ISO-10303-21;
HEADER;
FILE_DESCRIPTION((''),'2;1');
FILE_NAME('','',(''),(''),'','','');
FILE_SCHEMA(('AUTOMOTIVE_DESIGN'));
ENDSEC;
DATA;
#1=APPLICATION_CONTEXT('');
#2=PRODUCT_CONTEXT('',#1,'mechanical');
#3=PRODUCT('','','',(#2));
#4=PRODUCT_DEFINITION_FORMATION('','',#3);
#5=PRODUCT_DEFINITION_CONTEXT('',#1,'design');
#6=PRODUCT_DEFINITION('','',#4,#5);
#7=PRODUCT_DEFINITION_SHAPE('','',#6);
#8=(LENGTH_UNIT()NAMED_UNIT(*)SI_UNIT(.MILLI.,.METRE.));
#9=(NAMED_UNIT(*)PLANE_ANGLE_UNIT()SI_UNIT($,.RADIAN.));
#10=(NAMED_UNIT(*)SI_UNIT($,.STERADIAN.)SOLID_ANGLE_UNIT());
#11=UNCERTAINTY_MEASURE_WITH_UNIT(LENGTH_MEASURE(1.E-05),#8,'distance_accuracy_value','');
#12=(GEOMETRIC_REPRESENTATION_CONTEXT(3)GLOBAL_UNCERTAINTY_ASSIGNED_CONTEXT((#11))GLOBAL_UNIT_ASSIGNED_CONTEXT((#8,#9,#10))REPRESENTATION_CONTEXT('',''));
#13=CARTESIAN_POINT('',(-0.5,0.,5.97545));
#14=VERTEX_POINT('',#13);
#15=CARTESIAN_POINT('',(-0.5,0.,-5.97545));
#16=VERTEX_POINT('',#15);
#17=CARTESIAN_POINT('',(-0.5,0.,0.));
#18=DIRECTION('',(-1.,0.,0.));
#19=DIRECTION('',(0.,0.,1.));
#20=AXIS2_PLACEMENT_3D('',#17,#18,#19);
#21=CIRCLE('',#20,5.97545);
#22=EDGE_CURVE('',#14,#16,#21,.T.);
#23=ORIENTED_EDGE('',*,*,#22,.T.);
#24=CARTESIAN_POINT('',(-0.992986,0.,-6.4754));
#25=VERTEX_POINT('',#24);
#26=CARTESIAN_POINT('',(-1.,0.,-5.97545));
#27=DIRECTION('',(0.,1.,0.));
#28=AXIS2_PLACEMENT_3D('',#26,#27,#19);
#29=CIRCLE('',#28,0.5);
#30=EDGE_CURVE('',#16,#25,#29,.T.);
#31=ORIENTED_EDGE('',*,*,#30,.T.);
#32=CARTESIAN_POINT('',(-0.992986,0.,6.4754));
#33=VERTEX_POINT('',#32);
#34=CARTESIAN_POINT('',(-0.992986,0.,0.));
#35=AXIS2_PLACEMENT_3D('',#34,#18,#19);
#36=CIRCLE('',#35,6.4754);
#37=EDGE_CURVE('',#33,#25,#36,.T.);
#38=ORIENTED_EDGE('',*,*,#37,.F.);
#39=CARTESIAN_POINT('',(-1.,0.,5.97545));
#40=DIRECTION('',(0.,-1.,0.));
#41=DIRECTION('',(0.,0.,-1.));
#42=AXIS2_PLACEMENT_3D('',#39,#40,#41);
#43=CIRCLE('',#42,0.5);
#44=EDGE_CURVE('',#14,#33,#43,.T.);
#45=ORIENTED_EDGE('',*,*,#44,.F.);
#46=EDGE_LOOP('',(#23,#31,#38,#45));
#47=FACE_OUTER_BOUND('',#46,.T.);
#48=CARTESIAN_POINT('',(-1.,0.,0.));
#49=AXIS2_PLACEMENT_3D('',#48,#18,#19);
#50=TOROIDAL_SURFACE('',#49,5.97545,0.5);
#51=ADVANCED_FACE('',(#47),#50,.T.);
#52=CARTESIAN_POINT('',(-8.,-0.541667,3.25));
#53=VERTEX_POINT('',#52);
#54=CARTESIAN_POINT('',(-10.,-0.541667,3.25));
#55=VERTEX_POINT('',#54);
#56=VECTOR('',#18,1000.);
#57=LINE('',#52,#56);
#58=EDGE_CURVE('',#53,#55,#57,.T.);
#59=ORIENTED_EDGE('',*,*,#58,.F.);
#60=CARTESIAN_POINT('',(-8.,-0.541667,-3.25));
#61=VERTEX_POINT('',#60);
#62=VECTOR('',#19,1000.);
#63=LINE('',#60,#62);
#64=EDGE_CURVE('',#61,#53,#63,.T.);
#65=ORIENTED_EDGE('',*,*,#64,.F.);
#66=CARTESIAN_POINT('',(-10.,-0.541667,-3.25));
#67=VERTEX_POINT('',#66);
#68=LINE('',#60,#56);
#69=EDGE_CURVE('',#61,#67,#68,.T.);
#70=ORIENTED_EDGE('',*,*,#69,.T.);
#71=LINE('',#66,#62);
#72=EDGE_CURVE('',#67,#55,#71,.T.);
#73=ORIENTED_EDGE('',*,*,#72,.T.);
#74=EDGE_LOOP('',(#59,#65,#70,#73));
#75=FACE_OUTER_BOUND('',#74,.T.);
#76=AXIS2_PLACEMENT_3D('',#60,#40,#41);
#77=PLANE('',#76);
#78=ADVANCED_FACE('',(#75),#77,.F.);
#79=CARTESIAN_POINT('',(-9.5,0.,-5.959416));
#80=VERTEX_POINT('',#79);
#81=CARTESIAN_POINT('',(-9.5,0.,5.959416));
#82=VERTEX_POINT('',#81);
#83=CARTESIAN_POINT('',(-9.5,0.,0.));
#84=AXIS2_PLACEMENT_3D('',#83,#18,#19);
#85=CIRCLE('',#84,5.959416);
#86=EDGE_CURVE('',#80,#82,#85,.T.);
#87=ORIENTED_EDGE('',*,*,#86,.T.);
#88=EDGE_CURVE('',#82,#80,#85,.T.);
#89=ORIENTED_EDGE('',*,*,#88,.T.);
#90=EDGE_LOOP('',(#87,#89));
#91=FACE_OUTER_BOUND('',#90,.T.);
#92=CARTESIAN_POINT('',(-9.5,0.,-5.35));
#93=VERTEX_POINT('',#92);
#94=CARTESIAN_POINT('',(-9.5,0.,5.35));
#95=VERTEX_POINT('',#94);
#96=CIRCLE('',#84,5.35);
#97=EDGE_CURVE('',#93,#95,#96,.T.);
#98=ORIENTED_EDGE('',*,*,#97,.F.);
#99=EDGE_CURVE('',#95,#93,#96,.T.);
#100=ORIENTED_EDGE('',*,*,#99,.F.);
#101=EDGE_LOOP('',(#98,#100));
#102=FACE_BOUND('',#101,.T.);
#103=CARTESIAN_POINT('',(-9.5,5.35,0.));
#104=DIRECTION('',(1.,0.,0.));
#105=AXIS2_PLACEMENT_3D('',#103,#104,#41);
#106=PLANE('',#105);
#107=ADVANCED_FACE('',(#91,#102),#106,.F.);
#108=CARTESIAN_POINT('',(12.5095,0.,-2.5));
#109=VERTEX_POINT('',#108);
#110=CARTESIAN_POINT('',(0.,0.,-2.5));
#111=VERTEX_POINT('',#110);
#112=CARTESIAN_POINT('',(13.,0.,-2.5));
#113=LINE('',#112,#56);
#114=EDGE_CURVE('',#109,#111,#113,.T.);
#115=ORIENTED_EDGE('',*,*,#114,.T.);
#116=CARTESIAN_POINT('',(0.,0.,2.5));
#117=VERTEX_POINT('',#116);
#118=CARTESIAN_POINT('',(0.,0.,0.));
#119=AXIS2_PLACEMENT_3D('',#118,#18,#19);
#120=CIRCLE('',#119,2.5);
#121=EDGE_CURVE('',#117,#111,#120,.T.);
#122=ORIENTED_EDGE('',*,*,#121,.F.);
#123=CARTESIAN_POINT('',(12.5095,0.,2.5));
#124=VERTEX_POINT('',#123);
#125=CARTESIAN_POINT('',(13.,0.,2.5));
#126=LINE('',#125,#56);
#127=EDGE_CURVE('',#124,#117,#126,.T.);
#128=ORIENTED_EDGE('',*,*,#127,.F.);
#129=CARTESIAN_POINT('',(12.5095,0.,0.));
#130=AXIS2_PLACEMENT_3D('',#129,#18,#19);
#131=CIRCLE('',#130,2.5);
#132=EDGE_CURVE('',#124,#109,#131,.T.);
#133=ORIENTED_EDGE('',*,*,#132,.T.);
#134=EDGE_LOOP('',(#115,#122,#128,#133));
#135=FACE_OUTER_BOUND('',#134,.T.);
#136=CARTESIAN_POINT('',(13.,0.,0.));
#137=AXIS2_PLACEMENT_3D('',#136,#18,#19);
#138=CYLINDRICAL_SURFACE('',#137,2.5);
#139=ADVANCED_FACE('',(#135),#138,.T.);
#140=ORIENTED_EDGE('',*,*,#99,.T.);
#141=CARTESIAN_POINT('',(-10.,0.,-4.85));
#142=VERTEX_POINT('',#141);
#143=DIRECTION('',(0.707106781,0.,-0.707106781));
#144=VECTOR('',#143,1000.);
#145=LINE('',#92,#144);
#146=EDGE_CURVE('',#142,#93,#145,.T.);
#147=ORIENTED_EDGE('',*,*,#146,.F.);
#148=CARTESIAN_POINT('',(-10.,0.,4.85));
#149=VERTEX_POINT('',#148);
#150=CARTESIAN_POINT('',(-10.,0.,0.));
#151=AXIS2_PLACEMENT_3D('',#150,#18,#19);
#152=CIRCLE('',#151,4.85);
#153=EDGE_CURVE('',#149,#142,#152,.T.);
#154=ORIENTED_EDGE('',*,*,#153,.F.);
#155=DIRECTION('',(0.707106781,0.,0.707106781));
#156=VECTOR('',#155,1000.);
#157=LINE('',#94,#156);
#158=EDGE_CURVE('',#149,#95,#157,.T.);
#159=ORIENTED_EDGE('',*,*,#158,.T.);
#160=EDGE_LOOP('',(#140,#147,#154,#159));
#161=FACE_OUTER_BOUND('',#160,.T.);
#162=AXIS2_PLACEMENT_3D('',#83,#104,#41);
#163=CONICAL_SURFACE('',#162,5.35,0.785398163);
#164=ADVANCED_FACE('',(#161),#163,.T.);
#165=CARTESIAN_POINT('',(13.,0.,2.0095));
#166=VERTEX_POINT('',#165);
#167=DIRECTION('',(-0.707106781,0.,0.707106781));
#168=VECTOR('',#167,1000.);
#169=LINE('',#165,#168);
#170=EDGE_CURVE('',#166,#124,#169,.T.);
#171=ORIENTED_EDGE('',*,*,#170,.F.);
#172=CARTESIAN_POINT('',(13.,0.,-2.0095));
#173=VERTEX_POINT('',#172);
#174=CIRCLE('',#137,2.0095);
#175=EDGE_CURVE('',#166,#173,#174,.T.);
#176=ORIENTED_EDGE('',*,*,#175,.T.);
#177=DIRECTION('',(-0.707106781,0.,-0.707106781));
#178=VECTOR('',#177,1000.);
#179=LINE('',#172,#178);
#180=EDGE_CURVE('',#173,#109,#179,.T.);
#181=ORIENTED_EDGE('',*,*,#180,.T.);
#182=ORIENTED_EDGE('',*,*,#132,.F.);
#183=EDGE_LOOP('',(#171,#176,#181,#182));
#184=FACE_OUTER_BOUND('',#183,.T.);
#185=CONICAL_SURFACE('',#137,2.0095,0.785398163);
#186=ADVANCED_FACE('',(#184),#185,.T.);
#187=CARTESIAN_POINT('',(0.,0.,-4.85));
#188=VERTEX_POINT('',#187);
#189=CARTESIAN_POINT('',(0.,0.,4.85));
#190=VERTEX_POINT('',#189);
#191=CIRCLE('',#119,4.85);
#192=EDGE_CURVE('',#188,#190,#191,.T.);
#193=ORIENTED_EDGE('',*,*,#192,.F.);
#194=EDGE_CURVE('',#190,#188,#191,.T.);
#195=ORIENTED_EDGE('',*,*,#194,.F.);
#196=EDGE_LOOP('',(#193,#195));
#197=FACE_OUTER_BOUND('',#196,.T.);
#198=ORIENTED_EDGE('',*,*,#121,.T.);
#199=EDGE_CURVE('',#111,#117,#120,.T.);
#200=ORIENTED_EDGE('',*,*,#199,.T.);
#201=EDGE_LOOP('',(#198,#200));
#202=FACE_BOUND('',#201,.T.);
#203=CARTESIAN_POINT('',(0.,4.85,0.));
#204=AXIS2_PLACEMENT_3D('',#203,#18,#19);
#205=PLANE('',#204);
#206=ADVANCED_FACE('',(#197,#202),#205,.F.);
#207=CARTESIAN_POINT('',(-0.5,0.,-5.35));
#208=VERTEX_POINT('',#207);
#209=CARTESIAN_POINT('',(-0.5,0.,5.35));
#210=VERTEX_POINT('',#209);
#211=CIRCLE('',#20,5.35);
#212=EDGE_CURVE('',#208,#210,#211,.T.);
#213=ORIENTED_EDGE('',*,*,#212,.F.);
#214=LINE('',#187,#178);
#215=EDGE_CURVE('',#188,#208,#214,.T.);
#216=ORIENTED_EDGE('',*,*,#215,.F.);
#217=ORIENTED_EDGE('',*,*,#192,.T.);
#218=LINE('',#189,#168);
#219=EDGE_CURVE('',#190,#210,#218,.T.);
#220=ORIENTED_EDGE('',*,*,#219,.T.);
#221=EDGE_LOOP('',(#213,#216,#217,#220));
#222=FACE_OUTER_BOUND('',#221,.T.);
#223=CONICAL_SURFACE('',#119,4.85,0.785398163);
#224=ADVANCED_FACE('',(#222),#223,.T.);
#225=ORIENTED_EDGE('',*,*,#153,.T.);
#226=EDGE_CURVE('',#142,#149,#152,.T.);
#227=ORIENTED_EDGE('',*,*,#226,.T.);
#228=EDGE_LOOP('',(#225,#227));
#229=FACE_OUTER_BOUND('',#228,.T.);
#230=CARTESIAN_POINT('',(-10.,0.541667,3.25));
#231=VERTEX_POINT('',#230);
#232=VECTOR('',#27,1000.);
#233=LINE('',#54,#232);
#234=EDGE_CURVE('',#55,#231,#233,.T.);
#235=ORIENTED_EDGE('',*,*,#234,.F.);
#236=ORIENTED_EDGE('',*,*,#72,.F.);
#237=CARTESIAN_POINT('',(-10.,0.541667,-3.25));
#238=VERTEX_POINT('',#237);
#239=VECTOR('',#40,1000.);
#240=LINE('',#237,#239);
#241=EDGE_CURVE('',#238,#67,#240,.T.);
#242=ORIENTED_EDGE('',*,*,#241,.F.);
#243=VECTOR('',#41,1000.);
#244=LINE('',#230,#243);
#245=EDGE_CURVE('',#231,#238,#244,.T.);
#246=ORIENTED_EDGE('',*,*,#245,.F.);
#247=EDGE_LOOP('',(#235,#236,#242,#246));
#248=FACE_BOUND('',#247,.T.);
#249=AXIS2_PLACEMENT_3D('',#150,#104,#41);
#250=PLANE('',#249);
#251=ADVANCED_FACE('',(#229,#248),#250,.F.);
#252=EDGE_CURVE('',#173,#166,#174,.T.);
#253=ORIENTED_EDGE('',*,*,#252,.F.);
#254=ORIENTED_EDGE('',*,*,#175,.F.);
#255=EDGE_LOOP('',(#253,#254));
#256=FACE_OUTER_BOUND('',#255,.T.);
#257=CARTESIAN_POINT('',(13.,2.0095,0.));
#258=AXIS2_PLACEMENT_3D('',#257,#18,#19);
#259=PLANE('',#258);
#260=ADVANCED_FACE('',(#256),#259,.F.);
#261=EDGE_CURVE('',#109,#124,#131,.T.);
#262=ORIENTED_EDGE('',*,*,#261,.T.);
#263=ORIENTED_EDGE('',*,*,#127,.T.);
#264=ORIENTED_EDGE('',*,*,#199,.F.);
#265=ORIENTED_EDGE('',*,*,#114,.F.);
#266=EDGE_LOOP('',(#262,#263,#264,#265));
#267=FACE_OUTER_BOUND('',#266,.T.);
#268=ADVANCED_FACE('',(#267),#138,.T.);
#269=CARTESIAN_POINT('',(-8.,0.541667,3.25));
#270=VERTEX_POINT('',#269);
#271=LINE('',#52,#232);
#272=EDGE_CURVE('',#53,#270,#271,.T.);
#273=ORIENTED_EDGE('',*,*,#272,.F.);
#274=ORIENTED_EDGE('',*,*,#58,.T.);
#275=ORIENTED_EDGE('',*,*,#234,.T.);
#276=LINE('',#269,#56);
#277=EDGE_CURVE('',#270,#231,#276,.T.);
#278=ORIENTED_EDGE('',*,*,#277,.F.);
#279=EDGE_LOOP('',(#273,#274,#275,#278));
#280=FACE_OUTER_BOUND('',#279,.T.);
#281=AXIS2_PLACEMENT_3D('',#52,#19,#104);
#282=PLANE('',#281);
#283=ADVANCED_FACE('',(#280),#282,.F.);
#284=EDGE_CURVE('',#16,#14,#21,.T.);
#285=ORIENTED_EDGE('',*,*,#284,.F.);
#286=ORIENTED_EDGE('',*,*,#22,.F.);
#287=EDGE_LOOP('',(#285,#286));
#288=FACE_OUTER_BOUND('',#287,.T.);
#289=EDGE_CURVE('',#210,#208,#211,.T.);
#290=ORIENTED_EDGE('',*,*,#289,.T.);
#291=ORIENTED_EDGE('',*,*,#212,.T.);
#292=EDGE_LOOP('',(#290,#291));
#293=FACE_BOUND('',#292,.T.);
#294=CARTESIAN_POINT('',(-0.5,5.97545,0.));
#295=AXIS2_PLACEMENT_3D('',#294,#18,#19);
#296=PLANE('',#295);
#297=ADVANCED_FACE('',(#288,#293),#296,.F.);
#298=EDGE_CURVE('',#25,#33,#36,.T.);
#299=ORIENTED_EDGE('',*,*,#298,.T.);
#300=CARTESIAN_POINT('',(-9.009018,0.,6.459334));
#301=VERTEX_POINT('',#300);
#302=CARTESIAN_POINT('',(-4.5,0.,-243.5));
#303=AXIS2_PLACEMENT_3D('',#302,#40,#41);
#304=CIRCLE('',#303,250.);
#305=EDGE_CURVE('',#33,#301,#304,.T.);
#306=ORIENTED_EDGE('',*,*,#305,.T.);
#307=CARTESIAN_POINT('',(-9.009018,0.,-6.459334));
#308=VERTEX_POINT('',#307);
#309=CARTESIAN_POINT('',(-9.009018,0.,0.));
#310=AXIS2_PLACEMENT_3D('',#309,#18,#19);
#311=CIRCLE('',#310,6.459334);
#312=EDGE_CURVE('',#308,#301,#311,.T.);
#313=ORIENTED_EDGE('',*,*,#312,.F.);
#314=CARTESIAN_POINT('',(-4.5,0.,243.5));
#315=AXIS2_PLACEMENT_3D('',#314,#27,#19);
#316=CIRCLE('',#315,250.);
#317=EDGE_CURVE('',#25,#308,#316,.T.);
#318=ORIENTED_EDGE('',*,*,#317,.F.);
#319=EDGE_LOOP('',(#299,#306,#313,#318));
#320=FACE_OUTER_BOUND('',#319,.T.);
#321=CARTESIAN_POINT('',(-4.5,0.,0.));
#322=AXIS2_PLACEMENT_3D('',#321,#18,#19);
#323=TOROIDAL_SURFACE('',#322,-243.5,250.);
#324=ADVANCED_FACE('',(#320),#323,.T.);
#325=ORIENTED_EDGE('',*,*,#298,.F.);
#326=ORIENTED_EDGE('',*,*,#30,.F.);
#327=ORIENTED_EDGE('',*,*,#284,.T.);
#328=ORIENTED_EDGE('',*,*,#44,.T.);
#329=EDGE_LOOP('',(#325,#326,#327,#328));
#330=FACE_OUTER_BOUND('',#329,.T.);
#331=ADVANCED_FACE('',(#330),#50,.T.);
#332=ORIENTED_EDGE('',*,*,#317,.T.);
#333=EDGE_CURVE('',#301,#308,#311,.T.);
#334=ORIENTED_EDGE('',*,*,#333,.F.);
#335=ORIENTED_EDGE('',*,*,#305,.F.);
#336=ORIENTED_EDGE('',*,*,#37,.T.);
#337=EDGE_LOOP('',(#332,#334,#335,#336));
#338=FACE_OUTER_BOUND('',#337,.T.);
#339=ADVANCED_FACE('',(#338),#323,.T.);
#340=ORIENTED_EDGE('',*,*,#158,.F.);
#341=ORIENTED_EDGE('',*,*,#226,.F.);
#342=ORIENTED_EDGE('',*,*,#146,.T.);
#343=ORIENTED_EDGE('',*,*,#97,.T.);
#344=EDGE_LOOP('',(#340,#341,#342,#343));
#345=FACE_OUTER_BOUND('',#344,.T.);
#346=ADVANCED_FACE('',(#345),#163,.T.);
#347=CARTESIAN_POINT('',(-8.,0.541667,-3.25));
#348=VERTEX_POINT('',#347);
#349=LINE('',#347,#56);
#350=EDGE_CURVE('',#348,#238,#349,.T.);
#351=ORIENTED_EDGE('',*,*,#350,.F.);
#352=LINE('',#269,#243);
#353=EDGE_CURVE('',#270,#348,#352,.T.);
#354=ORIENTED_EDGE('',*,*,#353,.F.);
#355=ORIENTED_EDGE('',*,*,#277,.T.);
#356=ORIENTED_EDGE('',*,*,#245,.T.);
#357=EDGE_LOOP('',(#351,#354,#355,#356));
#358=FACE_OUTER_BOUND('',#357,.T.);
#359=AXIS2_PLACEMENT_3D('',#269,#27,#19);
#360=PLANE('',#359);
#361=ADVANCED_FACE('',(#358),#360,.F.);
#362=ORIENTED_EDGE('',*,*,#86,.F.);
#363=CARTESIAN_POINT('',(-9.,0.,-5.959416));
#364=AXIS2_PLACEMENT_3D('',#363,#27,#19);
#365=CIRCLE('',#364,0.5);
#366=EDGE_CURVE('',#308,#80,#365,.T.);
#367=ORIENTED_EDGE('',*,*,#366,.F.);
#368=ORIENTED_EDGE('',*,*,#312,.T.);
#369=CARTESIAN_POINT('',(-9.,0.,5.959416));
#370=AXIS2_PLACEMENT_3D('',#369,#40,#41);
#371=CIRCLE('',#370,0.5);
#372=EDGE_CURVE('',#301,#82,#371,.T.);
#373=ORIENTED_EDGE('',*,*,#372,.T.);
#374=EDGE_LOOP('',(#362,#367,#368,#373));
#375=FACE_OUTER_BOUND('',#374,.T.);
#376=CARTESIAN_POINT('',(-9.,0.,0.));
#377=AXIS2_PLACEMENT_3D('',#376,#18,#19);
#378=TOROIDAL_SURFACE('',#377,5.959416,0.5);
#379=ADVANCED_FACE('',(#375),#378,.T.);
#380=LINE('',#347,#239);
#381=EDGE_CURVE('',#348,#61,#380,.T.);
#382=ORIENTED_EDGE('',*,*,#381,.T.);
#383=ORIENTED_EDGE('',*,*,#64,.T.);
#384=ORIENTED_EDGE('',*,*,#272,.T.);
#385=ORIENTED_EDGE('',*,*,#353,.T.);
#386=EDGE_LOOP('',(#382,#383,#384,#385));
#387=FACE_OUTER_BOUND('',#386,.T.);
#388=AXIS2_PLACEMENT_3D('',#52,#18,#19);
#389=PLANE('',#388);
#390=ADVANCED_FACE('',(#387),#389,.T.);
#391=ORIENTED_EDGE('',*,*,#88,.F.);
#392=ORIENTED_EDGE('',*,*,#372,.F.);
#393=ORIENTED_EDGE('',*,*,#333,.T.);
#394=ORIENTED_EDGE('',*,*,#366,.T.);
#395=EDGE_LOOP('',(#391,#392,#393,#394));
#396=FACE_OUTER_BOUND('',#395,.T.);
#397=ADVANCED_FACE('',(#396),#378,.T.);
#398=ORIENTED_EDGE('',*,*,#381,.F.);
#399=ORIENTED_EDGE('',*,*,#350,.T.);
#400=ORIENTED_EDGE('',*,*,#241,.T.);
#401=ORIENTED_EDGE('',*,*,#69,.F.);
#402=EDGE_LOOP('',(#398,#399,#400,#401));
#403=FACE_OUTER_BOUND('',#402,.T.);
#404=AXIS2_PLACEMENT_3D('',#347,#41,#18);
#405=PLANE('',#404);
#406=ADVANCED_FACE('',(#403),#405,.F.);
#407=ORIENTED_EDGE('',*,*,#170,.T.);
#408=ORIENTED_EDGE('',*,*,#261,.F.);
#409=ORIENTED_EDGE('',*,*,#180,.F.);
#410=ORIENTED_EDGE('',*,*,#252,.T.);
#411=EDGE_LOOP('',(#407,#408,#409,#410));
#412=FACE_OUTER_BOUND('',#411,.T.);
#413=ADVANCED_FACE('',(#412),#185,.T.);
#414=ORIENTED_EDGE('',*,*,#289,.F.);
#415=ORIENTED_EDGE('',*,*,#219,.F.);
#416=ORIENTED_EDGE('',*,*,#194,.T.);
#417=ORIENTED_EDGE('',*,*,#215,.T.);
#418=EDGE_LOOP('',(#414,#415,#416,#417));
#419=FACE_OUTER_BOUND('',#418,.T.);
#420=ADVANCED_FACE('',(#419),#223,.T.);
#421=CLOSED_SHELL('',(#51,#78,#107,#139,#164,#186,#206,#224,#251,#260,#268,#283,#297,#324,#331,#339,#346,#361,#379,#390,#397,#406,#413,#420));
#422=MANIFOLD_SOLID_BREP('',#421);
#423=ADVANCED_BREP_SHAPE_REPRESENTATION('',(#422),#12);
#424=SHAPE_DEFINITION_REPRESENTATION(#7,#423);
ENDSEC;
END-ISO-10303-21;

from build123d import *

# Parameters (mm, degrees)
SKETCH2_W          = 6.5
SKETCH2_H          = 1.083333334
CUT_EXTRUDE1_DEPTH = 2


with BuildPart() as part:
    # Sketch1 → Revolve1 (revolve)
    with BuildSketch(Plane.XY, mode=Mode.PRIVATE) as revolve1_sk:
        with BuildLine():
            Line((-10, 0), (-10, 4.85))
            Line((-10, 4.85), (-9.5, 5.35))
            Line((-9.5, 5.35), (-9.5, 5.959415537))
            ThreePointArc((-9.5, 5.959415537), (-9.3567275, 6.309766063), (-9.009018036, 6.459334205))
            ThreePointArc((-9.009018036, 6.459334205), (-5.001066402, 6.499497864), (-0.992985972, 6.475400495))
            ThreePointArc((-0.992985972, 6.475400495), (-0.643975412, 6.326514493), (-0.5, 5.975449694))
            Line((-0.5, 5.975449694), (-0.5, 5.35))
            Line((-0.5, 5.35), (0, 4.85))
            Line((0, 4.85), (0, 2.5))
            Line((0, 2.5), (12.5095, 2.5))
            Line((12.5095, 2.5), (13, 2.0095))
            Line((13, 2.0095), (13, 0))
            Line((13, 0), (-10, 0))
        make_face()
    revolve(revolve1_sk.sketch.rotate(Axis((13, 0, 0), (-1, 0, 0)), 270), axis=Axis((13, 0, 0), (-1, 0, 0)))

    # Sketch2 → Cut-Extrude1 (cut)
    with BuildSketch(Plane.ZY.offset(10)):
        Rectangle(SKETCH2_W, SKETCH2_H)
    extrude(amount=-CUT_EXTRUDE1_DEPTH, mode=Mode.SUBTRACT)


solid = part.part
